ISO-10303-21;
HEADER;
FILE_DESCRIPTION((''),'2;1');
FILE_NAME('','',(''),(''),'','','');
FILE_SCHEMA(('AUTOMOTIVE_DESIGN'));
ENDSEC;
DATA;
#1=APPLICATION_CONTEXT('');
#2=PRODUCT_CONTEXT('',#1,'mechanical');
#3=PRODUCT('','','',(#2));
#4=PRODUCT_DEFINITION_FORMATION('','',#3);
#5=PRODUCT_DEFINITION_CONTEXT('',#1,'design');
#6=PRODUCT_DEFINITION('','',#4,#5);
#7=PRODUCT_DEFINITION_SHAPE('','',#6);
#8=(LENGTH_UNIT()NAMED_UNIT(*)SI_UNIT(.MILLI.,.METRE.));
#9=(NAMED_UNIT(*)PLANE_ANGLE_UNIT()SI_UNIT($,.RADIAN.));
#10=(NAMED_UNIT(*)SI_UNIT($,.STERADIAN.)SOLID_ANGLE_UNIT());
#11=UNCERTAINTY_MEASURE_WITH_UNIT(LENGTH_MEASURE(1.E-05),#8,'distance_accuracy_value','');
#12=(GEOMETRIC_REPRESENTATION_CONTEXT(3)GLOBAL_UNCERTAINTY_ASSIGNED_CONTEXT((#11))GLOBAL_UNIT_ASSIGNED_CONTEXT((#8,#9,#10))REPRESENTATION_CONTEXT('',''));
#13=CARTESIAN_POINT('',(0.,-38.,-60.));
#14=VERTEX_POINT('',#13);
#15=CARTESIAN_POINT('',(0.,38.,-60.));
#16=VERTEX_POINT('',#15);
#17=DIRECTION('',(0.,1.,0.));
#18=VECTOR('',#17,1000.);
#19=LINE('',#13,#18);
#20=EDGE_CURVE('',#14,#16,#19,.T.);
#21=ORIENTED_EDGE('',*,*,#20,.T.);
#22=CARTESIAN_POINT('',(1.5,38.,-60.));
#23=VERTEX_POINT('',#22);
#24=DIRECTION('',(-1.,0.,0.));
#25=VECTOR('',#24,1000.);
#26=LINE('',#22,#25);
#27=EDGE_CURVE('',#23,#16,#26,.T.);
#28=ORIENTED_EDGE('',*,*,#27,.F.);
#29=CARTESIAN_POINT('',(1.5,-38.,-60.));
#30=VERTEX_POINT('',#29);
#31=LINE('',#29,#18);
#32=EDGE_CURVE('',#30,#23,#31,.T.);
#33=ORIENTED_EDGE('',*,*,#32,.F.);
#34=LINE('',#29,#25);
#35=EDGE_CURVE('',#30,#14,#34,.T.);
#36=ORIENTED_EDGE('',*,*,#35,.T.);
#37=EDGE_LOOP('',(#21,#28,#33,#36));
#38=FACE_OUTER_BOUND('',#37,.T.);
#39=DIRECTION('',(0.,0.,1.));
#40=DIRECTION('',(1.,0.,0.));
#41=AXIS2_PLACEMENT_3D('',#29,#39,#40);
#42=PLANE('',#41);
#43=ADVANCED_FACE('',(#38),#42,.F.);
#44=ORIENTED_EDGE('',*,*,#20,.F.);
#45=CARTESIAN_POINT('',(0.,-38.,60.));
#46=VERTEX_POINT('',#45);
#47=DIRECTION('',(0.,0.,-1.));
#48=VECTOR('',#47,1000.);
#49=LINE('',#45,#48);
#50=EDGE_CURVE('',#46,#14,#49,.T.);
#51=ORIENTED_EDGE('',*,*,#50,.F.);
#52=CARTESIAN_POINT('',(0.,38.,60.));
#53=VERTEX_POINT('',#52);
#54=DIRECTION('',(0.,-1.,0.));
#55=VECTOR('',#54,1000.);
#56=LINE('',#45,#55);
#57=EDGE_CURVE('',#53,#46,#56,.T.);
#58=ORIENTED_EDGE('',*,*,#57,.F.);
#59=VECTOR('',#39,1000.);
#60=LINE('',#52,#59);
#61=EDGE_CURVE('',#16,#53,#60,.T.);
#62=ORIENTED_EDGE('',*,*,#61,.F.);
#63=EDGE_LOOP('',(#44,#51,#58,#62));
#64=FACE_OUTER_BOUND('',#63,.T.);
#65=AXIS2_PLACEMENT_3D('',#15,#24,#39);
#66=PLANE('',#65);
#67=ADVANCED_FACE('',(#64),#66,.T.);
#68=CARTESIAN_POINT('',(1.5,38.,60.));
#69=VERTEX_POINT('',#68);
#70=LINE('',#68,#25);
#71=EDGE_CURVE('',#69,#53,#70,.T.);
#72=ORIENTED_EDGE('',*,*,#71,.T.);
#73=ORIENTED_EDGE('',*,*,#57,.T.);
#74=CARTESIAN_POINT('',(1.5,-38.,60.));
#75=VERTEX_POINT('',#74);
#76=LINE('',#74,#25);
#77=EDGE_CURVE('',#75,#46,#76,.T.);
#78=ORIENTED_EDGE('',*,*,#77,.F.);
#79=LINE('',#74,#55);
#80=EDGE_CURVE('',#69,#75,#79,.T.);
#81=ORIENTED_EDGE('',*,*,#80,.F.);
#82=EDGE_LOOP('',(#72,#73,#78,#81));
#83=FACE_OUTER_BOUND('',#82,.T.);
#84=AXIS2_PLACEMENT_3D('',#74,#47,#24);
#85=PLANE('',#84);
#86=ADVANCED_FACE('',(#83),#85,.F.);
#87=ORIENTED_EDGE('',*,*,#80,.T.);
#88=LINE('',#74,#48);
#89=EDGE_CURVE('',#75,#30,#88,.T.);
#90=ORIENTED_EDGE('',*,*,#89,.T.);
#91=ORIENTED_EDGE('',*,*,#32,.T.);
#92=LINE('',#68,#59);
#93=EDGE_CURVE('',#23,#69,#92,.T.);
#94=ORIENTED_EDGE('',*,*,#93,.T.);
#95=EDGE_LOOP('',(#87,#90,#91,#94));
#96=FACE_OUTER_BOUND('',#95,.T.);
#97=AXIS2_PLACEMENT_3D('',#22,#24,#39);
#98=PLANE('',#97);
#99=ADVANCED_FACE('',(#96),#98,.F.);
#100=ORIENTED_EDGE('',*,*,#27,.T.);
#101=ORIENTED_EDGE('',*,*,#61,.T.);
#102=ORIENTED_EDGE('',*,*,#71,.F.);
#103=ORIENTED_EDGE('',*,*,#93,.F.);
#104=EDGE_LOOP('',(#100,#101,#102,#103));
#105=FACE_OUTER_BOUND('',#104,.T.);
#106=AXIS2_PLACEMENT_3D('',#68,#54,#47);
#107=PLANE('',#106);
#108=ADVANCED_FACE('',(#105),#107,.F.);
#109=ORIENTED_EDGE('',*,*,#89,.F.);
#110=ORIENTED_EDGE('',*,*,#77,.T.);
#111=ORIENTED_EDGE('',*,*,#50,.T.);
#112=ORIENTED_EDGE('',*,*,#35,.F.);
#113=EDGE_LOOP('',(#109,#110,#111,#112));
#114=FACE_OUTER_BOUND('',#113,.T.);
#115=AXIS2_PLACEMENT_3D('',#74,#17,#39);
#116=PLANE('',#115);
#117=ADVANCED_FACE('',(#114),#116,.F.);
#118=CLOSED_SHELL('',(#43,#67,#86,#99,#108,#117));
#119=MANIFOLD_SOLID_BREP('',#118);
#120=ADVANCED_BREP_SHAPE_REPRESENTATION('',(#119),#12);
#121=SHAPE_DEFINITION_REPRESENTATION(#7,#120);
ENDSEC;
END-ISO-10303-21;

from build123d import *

# Parameters (mm, degrees)
SKETCH_1_W           = 120
SKETCH_1_H           = 76
BOSS_EXTRUDE_1_DEPTH = 1.5


with BuildPart() as part:
    # Sketch 1 → Boss-Extrude 1 (new body)
    with BuildSketch(Plane(origin=(0, 0, 0), x_dir=(0, 0, -1), z_dir=(1, 0, 0))):
        Rectangle(SKETCH_1_W, SKETCH_1_H)
    extrude(amount=BOSS_EXTRUDE_1_DEPTH)


solid = part.part
